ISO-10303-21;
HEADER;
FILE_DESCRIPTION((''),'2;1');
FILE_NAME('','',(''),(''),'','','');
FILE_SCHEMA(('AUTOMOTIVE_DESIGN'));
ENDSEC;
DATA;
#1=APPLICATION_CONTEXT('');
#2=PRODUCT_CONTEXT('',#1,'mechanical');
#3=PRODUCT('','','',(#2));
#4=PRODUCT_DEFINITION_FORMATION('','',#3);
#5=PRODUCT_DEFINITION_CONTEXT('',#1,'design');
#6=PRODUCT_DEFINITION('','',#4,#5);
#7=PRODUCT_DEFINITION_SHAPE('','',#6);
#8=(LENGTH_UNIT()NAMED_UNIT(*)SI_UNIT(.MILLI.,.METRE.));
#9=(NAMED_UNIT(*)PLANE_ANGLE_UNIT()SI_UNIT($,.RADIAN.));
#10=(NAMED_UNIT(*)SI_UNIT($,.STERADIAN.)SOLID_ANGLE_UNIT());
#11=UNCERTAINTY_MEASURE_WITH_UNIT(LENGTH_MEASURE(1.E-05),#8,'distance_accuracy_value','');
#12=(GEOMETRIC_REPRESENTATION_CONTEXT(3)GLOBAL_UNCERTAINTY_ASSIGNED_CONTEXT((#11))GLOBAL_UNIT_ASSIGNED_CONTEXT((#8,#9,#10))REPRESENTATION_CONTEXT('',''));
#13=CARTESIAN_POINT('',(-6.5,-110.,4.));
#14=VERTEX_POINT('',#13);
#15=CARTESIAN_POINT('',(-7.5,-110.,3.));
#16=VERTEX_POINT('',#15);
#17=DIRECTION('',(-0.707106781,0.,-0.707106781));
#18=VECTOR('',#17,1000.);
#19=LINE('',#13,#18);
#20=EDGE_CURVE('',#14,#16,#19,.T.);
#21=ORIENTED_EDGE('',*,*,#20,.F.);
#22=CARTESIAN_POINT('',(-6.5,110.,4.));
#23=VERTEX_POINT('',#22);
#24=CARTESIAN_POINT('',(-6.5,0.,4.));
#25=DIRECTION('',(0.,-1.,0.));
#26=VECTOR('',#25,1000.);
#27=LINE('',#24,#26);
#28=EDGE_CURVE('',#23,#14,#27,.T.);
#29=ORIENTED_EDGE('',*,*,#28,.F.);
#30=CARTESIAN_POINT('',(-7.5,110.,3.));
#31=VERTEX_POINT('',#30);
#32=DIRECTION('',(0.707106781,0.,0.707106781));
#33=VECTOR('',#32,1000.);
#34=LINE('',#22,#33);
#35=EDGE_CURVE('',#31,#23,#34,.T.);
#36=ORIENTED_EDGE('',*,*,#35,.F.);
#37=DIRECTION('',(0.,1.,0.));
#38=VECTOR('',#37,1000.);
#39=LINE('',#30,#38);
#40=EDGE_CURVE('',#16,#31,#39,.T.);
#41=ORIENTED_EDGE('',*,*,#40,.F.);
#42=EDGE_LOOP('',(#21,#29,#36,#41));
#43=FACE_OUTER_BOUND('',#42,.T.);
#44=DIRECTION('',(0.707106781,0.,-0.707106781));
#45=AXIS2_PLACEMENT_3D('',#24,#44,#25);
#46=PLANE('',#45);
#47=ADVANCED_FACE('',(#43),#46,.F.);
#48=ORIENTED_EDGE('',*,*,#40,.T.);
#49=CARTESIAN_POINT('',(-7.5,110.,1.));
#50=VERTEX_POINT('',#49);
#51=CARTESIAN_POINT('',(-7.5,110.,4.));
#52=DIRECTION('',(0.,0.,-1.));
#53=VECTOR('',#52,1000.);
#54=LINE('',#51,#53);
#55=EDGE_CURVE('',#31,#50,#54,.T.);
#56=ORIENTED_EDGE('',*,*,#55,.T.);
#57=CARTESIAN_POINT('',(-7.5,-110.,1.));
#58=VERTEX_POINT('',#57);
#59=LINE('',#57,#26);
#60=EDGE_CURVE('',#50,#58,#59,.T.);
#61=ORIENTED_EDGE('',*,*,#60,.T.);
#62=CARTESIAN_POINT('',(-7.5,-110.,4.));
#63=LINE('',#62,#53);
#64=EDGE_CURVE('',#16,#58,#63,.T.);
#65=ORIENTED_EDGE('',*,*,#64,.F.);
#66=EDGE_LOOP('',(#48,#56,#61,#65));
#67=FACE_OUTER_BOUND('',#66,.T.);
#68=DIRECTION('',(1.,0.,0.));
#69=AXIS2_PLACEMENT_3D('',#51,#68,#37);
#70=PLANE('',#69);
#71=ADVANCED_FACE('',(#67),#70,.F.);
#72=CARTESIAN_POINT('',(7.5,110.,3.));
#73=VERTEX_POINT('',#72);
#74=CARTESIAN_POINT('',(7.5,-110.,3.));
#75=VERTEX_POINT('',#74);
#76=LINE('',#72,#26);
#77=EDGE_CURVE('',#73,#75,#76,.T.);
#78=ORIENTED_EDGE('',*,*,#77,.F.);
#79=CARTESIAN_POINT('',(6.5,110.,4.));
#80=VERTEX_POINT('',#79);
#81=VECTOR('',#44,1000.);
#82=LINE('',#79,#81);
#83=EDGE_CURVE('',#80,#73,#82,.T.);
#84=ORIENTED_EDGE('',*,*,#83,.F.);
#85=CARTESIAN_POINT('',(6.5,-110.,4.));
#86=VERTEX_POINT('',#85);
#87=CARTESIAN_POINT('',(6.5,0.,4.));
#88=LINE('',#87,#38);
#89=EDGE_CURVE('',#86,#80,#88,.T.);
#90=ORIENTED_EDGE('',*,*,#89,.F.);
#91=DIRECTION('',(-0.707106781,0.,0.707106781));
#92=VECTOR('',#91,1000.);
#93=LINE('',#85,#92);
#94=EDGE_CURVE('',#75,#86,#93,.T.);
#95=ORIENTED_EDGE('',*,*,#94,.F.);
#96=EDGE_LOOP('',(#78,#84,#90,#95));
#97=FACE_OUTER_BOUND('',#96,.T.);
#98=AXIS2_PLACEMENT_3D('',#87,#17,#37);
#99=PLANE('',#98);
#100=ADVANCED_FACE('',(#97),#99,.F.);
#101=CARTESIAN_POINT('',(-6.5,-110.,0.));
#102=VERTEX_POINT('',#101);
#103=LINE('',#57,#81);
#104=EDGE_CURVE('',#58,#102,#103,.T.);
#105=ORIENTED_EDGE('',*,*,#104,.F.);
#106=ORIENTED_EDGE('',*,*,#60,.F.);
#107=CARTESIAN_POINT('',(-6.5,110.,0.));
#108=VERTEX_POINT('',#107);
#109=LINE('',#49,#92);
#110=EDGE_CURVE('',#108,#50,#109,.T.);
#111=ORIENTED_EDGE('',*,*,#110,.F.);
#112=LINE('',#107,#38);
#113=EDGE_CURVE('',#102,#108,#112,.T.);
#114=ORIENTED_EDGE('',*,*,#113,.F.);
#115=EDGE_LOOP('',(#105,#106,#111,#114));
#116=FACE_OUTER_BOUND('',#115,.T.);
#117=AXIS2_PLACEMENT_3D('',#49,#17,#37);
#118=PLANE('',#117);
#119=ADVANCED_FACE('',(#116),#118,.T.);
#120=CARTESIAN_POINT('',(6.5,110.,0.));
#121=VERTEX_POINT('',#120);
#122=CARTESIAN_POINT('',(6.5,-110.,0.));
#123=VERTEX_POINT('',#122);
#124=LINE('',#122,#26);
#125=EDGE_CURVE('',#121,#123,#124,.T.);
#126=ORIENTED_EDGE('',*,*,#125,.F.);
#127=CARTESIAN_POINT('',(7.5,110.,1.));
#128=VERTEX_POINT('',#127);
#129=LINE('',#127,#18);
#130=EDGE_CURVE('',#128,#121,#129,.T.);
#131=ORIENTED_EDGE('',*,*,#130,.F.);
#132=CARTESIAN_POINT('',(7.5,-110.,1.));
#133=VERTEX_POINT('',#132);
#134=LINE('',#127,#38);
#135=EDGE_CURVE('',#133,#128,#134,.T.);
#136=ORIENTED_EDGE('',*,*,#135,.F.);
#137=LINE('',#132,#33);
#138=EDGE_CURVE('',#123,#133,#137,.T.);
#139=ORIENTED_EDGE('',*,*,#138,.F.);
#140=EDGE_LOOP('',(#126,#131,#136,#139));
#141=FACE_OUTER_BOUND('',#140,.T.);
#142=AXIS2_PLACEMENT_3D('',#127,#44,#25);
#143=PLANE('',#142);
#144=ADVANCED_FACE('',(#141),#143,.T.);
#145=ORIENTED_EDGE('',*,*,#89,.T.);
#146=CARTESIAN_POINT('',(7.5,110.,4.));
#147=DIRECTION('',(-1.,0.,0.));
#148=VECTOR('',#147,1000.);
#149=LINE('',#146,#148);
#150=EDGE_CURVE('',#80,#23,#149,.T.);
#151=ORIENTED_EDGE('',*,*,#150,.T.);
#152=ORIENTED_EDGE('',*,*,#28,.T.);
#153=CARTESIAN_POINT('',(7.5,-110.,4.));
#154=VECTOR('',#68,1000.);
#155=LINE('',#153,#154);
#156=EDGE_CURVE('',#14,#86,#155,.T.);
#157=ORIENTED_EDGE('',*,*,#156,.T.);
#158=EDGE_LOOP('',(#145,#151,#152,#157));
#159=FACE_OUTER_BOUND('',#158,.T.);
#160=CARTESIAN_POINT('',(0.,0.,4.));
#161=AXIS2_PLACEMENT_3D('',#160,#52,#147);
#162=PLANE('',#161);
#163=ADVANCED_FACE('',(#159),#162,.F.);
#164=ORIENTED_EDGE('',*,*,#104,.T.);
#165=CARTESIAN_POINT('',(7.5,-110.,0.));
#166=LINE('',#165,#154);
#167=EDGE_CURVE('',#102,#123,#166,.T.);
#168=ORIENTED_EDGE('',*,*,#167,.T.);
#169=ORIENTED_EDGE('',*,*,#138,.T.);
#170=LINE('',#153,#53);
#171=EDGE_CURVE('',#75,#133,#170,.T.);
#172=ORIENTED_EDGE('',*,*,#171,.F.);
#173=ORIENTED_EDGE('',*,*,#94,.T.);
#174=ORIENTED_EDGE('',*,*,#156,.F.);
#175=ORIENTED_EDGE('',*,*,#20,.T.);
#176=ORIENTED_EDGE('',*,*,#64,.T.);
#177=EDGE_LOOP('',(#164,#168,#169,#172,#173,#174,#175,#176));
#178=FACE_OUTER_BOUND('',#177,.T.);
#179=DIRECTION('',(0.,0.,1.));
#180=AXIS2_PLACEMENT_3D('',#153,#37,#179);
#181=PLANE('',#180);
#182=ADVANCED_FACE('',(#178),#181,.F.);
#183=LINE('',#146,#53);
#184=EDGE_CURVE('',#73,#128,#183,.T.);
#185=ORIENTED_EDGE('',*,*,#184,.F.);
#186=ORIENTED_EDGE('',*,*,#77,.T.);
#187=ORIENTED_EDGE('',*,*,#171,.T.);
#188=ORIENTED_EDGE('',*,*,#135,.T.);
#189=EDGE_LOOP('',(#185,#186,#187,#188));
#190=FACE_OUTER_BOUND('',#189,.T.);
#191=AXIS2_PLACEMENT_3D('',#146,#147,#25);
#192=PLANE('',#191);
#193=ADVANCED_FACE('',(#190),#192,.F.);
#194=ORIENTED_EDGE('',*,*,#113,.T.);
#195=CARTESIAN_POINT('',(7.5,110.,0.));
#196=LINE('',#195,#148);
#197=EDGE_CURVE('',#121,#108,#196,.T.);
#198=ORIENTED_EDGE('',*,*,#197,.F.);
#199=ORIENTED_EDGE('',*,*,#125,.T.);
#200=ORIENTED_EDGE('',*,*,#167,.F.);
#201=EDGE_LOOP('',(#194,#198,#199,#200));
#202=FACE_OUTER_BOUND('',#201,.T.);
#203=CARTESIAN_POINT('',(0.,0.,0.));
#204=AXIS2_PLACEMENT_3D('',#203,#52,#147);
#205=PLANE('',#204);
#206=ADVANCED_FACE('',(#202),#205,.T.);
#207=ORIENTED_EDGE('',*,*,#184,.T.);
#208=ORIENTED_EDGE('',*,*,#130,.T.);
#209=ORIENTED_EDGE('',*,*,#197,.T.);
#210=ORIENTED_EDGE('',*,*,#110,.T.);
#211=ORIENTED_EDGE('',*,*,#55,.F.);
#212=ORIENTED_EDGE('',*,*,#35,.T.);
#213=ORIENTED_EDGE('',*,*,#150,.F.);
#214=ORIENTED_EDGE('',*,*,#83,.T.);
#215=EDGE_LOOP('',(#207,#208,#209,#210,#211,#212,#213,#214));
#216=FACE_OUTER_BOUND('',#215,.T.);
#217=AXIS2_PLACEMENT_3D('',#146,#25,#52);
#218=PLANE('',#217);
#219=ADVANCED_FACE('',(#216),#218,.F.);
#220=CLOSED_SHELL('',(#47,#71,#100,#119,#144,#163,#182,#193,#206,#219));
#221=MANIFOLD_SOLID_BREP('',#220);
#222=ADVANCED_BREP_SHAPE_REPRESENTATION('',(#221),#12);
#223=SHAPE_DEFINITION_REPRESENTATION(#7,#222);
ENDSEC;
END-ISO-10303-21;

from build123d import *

# Parameters (mm, degrees)
SKETCH1_W           = 15
SKETCH1_H           = 220
BOSS_EXTRUDE1_DEPTH = 4
CHAMFER1_SIZE       = 1


with BuildPart() as part:
    # Sketch1 → Boss-Extrude1 (new body)
    with BuildSketch(Plane.XY):
        Rectangle(SKETCH1_W, SKETCH1_H)
    extrude(amount=BOSS_EXTRUDE1_DEPTH)

    # Chamfer1
    chamfer1_edges = [part.edges().sort_by_distance(p)[0] for p in [
        (7.5, 0, 4),
        (-7.5, 0, 4),
        (7.5, 0, 0),
        (-7.5, 0, 0),
    ]]
    chamfer(chamfer1_edges, length=CHAMFER1_SIZE)


solid = part.part
